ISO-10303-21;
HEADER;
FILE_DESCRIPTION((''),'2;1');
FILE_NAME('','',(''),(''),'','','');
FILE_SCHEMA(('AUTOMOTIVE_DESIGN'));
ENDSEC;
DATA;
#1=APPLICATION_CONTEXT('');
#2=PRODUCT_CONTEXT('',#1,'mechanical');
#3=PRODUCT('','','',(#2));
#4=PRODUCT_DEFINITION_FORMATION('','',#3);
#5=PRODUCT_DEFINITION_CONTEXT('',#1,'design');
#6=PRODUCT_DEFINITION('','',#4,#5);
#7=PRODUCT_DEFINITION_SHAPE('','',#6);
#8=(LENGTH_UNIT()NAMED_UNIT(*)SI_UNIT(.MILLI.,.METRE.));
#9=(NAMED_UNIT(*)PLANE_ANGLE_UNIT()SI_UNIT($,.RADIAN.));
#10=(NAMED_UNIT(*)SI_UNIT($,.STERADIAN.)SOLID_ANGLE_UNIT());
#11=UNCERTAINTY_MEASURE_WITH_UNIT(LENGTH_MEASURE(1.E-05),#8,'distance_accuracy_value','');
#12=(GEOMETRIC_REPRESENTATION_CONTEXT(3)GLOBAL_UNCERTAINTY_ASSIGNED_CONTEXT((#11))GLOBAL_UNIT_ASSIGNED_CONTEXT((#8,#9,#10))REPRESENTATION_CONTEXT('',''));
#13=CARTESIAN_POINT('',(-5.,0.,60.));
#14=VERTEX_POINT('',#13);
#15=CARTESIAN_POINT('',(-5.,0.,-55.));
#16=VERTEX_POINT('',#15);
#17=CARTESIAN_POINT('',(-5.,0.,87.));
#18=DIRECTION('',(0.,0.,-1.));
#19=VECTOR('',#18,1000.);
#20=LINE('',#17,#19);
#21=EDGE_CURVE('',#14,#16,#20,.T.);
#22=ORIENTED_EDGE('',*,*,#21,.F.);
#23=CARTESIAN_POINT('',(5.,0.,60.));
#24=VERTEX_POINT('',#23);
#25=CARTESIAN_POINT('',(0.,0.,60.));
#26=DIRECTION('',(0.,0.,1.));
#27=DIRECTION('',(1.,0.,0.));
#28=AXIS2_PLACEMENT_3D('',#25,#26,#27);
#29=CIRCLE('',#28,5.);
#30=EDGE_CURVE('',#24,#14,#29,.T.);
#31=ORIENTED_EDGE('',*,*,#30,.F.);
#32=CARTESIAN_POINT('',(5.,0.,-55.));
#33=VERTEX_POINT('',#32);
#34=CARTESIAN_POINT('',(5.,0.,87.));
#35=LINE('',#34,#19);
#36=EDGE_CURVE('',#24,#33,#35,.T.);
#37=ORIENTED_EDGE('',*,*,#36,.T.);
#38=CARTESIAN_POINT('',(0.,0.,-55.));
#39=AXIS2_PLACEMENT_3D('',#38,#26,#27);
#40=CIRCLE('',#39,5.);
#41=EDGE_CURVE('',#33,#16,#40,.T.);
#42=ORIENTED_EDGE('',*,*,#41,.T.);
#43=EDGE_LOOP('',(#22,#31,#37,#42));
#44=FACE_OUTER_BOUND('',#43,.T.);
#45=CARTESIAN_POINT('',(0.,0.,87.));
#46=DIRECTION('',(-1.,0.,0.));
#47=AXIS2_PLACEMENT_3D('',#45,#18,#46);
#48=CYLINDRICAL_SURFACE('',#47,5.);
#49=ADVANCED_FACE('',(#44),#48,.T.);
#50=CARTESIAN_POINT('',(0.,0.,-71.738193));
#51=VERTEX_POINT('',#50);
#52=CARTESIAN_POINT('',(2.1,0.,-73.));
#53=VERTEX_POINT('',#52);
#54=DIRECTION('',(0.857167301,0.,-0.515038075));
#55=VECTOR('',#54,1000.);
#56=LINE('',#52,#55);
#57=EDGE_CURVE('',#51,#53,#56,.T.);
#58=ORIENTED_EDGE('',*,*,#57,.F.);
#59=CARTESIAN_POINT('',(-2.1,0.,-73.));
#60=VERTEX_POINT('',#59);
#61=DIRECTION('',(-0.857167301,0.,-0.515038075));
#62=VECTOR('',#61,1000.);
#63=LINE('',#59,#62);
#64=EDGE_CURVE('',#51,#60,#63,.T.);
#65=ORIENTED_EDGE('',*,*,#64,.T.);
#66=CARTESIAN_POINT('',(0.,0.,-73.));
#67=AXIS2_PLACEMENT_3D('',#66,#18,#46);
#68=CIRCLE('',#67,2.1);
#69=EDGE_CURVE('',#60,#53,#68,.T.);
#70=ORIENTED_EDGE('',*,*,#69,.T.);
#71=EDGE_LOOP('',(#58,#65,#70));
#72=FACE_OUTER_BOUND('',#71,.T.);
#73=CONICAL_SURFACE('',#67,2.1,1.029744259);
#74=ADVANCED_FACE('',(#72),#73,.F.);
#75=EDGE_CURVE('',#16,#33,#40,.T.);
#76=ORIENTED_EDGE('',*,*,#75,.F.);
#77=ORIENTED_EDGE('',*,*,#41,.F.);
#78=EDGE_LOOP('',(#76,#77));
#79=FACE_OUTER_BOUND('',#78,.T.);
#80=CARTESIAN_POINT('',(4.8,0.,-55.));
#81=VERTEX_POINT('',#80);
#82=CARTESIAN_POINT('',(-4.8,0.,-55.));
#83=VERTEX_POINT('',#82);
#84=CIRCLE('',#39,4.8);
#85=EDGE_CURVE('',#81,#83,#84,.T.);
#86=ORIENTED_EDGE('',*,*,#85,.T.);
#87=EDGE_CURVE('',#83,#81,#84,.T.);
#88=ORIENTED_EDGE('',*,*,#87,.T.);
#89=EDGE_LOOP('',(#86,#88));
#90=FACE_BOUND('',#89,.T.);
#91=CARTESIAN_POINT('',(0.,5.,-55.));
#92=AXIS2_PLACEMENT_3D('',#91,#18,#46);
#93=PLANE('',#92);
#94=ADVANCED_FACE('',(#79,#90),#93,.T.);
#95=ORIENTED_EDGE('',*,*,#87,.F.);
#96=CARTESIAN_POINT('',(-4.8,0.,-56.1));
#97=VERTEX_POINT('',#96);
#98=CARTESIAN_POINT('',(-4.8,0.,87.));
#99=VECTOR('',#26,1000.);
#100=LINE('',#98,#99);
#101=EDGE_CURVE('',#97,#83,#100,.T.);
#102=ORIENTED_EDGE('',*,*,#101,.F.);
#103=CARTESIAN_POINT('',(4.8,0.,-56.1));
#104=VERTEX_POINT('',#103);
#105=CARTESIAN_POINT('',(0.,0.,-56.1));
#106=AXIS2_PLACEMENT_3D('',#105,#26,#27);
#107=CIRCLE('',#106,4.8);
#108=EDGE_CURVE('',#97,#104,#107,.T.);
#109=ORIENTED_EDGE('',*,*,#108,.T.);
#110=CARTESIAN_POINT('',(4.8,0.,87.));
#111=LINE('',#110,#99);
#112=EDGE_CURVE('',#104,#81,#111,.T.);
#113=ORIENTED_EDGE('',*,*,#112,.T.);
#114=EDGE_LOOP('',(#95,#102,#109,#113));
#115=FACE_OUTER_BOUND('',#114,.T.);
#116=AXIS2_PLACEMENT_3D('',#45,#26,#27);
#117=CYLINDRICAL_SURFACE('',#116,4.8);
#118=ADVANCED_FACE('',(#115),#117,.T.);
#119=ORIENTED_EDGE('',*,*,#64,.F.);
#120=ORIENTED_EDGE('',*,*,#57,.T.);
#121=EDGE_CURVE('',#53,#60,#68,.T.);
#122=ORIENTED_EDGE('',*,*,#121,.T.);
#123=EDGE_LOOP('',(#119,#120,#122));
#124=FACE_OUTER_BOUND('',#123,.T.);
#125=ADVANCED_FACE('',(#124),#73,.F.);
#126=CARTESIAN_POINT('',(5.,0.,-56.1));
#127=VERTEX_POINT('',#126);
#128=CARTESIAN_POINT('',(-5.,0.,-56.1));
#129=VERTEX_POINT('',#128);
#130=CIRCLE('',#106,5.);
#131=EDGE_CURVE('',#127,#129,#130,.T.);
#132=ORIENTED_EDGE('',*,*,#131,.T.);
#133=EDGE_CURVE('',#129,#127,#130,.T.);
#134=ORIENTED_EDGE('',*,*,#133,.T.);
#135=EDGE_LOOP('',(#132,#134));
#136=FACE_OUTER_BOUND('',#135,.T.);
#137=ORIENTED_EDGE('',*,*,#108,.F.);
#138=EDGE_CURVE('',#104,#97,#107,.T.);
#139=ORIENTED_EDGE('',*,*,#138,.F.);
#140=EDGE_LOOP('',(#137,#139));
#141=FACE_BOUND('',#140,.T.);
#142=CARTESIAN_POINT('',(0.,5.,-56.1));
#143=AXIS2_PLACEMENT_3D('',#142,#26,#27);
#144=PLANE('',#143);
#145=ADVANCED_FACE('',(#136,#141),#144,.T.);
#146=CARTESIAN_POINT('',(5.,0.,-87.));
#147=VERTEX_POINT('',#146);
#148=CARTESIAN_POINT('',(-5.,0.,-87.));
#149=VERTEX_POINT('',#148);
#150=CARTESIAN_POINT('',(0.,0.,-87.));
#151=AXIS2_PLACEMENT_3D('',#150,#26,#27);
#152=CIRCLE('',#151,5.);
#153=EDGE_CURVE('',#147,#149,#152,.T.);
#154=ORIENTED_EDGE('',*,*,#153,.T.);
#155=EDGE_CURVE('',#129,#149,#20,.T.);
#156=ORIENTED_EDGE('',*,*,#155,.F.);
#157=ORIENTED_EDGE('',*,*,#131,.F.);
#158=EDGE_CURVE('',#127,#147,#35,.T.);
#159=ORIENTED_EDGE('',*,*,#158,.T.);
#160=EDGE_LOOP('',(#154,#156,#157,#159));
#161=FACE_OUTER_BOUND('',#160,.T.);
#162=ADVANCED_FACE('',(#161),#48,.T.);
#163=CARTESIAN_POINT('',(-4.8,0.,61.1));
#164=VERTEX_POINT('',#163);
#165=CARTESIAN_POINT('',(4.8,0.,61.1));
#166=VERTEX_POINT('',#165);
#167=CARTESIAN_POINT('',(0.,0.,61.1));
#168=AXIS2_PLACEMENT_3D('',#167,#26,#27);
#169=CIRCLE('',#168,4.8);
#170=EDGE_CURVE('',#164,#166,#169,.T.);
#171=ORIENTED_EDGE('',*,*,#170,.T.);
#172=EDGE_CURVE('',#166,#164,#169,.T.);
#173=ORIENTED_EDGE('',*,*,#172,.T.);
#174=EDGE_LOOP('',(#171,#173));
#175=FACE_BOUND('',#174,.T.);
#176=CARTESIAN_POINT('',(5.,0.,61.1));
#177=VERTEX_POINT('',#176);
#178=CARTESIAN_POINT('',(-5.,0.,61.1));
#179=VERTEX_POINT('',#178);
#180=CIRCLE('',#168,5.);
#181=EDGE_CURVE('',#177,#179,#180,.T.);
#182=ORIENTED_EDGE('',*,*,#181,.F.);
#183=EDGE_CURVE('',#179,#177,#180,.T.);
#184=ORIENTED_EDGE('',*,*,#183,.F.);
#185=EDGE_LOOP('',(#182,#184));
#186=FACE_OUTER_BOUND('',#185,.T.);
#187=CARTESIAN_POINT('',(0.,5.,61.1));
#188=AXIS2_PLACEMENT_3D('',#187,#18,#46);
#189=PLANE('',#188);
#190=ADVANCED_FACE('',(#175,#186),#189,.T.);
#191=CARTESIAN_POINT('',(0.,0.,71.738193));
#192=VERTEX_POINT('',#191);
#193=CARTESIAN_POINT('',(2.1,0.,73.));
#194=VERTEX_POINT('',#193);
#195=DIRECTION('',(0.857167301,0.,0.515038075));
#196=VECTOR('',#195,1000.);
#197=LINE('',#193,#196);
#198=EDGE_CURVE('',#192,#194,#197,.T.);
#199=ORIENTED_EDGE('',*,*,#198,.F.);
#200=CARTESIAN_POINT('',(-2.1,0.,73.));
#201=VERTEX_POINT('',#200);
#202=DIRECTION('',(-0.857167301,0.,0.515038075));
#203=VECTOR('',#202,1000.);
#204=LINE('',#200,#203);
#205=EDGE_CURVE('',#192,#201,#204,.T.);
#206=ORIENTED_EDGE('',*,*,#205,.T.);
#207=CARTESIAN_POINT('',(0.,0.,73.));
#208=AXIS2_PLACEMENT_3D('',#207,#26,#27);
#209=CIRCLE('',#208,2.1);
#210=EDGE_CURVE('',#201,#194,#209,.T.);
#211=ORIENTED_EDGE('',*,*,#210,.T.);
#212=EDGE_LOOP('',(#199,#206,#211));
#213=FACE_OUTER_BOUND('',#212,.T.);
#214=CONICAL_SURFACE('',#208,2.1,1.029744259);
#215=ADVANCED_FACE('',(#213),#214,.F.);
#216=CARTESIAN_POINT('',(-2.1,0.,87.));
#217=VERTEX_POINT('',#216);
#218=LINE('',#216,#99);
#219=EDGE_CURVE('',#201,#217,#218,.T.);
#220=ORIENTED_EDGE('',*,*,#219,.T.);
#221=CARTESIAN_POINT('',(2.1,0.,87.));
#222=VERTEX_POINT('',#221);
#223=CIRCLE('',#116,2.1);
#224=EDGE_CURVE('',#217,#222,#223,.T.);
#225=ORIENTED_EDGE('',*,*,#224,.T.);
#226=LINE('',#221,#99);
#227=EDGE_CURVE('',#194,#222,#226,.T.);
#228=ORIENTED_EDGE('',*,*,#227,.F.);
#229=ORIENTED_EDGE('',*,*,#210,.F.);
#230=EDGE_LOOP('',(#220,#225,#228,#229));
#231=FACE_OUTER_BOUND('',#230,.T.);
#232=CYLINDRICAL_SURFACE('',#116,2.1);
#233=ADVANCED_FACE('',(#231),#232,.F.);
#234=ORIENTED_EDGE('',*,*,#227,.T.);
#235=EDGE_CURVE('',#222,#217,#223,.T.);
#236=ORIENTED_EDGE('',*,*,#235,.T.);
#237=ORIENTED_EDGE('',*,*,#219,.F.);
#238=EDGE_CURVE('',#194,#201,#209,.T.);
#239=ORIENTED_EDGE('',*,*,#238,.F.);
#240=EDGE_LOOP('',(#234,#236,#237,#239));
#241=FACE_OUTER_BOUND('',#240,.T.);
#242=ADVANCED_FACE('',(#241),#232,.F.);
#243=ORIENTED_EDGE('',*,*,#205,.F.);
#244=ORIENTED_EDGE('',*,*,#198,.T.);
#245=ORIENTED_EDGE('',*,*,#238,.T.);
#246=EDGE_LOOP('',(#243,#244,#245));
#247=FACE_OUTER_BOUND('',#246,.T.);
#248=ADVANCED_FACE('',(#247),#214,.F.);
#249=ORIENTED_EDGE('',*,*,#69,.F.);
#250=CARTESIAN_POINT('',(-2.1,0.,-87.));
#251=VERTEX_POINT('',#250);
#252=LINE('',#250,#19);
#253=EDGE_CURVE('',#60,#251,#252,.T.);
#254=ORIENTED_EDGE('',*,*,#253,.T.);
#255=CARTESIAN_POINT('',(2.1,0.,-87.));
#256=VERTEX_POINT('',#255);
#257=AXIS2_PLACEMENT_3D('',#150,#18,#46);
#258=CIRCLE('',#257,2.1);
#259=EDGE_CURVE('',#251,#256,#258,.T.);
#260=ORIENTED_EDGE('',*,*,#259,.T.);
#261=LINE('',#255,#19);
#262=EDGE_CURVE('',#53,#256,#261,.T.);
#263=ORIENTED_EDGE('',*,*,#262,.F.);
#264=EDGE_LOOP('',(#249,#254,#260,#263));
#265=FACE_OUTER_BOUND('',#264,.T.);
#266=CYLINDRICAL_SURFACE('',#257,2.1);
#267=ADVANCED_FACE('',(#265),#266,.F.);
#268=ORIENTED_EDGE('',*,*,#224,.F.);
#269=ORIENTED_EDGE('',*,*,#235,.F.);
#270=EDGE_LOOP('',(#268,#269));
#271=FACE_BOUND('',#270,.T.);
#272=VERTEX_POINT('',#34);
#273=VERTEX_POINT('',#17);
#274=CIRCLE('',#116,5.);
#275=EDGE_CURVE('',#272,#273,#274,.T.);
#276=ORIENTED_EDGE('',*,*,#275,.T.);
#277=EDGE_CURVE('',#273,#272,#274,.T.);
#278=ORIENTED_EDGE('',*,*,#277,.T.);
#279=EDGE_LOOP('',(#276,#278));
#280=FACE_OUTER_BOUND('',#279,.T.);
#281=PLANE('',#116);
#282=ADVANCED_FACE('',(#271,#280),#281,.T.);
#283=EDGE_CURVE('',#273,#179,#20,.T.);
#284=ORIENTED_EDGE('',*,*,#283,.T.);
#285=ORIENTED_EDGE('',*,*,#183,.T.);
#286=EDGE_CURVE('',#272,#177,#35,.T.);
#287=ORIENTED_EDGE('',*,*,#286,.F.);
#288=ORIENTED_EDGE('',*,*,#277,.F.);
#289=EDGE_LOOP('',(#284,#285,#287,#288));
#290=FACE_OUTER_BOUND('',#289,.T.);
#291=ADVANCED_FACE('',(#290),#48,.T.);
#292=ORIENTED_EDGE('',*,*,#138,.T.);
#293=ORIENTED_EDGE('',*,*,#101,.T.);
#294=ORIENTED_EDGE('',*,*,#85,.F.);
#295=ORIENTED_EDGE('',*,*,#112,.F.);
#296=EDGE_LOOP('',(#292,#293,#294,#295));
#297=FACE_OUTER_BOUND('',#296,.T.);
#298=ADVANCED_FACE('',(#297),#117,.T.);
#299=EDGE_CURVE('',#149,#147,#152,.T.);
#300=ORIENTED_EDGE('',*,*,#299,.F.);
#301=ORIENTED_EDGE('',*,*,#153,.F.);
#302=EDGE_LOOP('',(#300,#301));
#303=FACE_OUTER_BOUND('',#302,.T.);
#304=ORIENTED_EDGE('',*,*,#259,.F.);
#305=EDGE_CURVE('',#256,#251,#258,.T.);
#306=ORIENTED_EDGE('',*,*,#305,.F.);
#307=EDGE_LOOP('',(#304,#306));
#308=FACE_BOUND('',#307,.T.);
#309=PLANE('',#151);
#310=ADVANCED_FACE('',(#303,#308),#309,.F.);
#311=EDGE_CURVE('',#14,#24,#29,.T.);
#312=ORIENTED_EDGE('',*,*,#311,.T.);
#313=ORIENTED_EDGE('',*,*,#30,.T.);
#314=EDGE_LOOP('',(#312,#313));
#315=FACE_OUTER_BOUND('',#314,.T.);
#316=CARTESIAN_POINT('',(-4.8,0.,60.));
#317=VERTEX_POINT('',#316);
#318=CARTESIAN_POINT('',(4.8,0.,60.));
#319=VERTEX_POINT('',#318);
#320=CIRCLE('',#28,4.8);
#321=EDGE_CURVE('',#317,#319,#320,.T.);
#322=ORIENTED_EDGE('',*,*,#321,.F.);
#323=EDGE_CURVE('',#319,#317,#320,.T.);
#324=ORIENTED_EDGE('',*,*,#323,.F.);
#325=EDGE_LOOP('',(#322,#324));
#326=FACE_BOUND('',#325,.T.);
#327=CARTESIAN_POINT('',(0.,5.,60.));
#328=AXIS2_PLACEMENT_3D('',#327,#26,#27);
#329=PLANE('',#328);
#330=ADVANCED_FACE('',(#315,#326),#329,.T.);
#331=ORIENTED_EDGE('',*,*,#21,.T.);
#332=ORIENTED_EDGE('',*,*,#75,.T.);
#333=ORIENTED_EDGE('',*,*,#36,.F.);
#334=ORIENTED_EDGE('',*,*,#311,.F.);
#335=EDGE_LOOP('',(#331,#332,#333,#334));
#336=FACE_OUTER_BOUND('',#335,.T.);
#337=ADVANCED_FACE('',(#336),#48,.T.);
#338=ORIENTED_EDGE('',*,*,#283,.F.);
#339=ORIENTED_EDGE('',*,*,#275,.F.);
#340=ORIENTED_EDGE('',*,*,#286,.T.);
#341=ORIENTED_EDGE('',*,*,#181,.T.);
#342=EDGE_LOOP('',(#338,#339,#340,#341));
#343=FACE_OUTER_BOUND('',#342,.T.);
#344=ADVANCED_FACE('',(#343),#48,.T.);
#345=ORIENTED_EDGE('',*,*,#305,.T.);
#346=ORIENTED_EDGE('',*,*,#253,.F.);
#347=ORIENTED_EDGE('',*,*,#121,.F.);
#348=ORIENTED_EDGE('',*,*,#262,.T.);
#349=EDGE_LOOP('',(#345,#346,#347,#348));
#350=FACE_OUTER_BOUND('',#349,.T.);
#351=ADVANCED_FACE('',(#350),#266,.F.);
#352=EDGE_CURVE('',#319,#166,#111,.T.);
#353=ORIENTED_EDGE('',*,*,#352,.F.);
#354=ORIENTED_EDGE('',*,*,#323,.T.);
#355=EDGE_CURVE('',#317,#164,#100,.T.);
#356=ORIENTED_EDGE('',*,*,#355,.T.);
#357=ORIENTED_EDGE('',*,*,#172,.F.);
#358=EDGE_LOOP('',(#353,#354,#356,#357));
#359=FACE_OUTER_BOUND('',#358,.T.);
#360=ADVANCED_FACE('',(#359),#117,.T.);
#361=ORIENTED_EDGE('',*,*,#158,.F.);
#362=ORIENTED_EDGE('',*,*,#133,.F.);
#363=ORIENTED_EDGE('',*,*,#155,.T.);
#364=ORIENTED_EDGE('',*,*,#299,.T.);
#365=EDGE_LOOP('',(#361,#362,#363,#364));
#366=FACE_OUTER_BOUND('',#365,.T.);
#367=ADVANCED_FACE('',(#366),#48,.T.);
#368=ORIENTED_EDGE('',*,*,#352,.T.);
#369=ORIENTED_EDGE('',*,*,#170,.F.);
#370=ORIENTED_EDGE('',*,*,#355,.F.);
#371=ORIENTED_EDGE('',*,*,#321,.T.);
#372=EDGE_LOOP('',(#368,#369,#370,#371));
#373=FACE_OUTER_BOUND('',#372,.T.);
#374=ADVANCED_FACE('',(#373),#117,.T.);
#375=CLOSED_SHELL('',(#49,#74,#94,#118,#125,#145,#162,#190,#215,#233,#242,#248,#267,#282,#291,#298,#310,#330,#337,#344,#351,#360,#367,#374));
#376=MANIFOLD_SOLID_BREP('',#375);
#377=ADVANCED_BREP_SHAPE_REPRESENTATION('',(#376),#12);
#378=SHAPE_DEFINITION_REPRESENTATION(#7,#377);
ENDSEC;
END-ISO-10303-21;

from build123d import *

# Parameters (mm, degrees)
SKETCH1_R             = 5
BOSS_EXTRUDE1_DEPTH   = 87
M5_TAPPED_HOLE1_D     = 4.2
M5_TAPPED_HOLE1_DEPTH = 14
M5_TAPPED_HOLE1_TIP   = 1.2618073
M5_TAPPED_HOLE2_D     = 4.2
M5_TAPPED_HOLE2_DEPTH = 14
M5_TAPPED_HOLE2_TIP   = 1.2618073
SKETCH10_W            = 1.1
SKETCH10_H            = 0.2


with BuildPart() as part:
    # Sketch1 → Boss-Extrude1 (new, symmetric)
    with BuildSketch(Plane.XY):
        Circle(SKETCH1_R)
    extrude(amount=BOSS_EXTRUDE1_DEPTH, both=True)

    # M5 Tapped Hole1
    with Locations(Plane(origin=(0, 0, -87), x_dir=(-1, 0, 0), z_dir=(0, 0, -1))):
        with Locations((0, 0)):
            Hole(M5_TAPPED_HOLE1_D / 2, depth=M5_TAPPED_HOLE1_DEPTH)
            with Locations((0, 0, -(M5_TAPPED_HOLE1_DEPTH + M5_TAPPED_HOLE1_TIP / 2))):  # 118° drill point
                Cone(0, M5_TAPPED_HOLE1_D / 2, M5_TAPPED_HOLE1_TIP, mode=Mode.SUBTRACT)

    # M5 Tapped Hole2
    with Locations(Plane.XY.offset(87)):
        with Locations((0, 0)):
            Hole(M5_TAPPED_HOLE2_D / 2, depth=M5_TAPPED_HOLE2_DEPTH)
            with Locations((0, 0, -(M5_TAPPED_HOLE2_DEPTH + M5_TAPPED_HOLE2_TIP / 2))):  # 118° drill point
                Cone(0, M5_TAPPED_HOLE2_D / 2, M5_TAPPED_HOLE2_TIP, mode=Mode.SUBTRACT)

    # Sketch10 → Cut-Revolve1 (revolve, cut)
    with BuildSketch(Plane(origin=(0, 0, 0), x_dir=(0, 0, -1), z_dir=(1, 0, 0)), mode=Mode.PRIVATE) as cut_revolve1_sk:
        with Locations((-60.55, 4.9)):
            Rectangle(SKETCH10_W, SKETCH10_H)
        with Locations((55.55, 4.9)):
            Rectangle(SKETCH10_W, SKETCH10_H)
    revolve(cut_revolve1_sk.sketch.rotate(Axis((0, 0, 87), (0, 0, -1)), 90), axis=Axis((0, 0, 87), (0, 0, -1)), mode=Mode.SUBTRACT)


solid = part.part
